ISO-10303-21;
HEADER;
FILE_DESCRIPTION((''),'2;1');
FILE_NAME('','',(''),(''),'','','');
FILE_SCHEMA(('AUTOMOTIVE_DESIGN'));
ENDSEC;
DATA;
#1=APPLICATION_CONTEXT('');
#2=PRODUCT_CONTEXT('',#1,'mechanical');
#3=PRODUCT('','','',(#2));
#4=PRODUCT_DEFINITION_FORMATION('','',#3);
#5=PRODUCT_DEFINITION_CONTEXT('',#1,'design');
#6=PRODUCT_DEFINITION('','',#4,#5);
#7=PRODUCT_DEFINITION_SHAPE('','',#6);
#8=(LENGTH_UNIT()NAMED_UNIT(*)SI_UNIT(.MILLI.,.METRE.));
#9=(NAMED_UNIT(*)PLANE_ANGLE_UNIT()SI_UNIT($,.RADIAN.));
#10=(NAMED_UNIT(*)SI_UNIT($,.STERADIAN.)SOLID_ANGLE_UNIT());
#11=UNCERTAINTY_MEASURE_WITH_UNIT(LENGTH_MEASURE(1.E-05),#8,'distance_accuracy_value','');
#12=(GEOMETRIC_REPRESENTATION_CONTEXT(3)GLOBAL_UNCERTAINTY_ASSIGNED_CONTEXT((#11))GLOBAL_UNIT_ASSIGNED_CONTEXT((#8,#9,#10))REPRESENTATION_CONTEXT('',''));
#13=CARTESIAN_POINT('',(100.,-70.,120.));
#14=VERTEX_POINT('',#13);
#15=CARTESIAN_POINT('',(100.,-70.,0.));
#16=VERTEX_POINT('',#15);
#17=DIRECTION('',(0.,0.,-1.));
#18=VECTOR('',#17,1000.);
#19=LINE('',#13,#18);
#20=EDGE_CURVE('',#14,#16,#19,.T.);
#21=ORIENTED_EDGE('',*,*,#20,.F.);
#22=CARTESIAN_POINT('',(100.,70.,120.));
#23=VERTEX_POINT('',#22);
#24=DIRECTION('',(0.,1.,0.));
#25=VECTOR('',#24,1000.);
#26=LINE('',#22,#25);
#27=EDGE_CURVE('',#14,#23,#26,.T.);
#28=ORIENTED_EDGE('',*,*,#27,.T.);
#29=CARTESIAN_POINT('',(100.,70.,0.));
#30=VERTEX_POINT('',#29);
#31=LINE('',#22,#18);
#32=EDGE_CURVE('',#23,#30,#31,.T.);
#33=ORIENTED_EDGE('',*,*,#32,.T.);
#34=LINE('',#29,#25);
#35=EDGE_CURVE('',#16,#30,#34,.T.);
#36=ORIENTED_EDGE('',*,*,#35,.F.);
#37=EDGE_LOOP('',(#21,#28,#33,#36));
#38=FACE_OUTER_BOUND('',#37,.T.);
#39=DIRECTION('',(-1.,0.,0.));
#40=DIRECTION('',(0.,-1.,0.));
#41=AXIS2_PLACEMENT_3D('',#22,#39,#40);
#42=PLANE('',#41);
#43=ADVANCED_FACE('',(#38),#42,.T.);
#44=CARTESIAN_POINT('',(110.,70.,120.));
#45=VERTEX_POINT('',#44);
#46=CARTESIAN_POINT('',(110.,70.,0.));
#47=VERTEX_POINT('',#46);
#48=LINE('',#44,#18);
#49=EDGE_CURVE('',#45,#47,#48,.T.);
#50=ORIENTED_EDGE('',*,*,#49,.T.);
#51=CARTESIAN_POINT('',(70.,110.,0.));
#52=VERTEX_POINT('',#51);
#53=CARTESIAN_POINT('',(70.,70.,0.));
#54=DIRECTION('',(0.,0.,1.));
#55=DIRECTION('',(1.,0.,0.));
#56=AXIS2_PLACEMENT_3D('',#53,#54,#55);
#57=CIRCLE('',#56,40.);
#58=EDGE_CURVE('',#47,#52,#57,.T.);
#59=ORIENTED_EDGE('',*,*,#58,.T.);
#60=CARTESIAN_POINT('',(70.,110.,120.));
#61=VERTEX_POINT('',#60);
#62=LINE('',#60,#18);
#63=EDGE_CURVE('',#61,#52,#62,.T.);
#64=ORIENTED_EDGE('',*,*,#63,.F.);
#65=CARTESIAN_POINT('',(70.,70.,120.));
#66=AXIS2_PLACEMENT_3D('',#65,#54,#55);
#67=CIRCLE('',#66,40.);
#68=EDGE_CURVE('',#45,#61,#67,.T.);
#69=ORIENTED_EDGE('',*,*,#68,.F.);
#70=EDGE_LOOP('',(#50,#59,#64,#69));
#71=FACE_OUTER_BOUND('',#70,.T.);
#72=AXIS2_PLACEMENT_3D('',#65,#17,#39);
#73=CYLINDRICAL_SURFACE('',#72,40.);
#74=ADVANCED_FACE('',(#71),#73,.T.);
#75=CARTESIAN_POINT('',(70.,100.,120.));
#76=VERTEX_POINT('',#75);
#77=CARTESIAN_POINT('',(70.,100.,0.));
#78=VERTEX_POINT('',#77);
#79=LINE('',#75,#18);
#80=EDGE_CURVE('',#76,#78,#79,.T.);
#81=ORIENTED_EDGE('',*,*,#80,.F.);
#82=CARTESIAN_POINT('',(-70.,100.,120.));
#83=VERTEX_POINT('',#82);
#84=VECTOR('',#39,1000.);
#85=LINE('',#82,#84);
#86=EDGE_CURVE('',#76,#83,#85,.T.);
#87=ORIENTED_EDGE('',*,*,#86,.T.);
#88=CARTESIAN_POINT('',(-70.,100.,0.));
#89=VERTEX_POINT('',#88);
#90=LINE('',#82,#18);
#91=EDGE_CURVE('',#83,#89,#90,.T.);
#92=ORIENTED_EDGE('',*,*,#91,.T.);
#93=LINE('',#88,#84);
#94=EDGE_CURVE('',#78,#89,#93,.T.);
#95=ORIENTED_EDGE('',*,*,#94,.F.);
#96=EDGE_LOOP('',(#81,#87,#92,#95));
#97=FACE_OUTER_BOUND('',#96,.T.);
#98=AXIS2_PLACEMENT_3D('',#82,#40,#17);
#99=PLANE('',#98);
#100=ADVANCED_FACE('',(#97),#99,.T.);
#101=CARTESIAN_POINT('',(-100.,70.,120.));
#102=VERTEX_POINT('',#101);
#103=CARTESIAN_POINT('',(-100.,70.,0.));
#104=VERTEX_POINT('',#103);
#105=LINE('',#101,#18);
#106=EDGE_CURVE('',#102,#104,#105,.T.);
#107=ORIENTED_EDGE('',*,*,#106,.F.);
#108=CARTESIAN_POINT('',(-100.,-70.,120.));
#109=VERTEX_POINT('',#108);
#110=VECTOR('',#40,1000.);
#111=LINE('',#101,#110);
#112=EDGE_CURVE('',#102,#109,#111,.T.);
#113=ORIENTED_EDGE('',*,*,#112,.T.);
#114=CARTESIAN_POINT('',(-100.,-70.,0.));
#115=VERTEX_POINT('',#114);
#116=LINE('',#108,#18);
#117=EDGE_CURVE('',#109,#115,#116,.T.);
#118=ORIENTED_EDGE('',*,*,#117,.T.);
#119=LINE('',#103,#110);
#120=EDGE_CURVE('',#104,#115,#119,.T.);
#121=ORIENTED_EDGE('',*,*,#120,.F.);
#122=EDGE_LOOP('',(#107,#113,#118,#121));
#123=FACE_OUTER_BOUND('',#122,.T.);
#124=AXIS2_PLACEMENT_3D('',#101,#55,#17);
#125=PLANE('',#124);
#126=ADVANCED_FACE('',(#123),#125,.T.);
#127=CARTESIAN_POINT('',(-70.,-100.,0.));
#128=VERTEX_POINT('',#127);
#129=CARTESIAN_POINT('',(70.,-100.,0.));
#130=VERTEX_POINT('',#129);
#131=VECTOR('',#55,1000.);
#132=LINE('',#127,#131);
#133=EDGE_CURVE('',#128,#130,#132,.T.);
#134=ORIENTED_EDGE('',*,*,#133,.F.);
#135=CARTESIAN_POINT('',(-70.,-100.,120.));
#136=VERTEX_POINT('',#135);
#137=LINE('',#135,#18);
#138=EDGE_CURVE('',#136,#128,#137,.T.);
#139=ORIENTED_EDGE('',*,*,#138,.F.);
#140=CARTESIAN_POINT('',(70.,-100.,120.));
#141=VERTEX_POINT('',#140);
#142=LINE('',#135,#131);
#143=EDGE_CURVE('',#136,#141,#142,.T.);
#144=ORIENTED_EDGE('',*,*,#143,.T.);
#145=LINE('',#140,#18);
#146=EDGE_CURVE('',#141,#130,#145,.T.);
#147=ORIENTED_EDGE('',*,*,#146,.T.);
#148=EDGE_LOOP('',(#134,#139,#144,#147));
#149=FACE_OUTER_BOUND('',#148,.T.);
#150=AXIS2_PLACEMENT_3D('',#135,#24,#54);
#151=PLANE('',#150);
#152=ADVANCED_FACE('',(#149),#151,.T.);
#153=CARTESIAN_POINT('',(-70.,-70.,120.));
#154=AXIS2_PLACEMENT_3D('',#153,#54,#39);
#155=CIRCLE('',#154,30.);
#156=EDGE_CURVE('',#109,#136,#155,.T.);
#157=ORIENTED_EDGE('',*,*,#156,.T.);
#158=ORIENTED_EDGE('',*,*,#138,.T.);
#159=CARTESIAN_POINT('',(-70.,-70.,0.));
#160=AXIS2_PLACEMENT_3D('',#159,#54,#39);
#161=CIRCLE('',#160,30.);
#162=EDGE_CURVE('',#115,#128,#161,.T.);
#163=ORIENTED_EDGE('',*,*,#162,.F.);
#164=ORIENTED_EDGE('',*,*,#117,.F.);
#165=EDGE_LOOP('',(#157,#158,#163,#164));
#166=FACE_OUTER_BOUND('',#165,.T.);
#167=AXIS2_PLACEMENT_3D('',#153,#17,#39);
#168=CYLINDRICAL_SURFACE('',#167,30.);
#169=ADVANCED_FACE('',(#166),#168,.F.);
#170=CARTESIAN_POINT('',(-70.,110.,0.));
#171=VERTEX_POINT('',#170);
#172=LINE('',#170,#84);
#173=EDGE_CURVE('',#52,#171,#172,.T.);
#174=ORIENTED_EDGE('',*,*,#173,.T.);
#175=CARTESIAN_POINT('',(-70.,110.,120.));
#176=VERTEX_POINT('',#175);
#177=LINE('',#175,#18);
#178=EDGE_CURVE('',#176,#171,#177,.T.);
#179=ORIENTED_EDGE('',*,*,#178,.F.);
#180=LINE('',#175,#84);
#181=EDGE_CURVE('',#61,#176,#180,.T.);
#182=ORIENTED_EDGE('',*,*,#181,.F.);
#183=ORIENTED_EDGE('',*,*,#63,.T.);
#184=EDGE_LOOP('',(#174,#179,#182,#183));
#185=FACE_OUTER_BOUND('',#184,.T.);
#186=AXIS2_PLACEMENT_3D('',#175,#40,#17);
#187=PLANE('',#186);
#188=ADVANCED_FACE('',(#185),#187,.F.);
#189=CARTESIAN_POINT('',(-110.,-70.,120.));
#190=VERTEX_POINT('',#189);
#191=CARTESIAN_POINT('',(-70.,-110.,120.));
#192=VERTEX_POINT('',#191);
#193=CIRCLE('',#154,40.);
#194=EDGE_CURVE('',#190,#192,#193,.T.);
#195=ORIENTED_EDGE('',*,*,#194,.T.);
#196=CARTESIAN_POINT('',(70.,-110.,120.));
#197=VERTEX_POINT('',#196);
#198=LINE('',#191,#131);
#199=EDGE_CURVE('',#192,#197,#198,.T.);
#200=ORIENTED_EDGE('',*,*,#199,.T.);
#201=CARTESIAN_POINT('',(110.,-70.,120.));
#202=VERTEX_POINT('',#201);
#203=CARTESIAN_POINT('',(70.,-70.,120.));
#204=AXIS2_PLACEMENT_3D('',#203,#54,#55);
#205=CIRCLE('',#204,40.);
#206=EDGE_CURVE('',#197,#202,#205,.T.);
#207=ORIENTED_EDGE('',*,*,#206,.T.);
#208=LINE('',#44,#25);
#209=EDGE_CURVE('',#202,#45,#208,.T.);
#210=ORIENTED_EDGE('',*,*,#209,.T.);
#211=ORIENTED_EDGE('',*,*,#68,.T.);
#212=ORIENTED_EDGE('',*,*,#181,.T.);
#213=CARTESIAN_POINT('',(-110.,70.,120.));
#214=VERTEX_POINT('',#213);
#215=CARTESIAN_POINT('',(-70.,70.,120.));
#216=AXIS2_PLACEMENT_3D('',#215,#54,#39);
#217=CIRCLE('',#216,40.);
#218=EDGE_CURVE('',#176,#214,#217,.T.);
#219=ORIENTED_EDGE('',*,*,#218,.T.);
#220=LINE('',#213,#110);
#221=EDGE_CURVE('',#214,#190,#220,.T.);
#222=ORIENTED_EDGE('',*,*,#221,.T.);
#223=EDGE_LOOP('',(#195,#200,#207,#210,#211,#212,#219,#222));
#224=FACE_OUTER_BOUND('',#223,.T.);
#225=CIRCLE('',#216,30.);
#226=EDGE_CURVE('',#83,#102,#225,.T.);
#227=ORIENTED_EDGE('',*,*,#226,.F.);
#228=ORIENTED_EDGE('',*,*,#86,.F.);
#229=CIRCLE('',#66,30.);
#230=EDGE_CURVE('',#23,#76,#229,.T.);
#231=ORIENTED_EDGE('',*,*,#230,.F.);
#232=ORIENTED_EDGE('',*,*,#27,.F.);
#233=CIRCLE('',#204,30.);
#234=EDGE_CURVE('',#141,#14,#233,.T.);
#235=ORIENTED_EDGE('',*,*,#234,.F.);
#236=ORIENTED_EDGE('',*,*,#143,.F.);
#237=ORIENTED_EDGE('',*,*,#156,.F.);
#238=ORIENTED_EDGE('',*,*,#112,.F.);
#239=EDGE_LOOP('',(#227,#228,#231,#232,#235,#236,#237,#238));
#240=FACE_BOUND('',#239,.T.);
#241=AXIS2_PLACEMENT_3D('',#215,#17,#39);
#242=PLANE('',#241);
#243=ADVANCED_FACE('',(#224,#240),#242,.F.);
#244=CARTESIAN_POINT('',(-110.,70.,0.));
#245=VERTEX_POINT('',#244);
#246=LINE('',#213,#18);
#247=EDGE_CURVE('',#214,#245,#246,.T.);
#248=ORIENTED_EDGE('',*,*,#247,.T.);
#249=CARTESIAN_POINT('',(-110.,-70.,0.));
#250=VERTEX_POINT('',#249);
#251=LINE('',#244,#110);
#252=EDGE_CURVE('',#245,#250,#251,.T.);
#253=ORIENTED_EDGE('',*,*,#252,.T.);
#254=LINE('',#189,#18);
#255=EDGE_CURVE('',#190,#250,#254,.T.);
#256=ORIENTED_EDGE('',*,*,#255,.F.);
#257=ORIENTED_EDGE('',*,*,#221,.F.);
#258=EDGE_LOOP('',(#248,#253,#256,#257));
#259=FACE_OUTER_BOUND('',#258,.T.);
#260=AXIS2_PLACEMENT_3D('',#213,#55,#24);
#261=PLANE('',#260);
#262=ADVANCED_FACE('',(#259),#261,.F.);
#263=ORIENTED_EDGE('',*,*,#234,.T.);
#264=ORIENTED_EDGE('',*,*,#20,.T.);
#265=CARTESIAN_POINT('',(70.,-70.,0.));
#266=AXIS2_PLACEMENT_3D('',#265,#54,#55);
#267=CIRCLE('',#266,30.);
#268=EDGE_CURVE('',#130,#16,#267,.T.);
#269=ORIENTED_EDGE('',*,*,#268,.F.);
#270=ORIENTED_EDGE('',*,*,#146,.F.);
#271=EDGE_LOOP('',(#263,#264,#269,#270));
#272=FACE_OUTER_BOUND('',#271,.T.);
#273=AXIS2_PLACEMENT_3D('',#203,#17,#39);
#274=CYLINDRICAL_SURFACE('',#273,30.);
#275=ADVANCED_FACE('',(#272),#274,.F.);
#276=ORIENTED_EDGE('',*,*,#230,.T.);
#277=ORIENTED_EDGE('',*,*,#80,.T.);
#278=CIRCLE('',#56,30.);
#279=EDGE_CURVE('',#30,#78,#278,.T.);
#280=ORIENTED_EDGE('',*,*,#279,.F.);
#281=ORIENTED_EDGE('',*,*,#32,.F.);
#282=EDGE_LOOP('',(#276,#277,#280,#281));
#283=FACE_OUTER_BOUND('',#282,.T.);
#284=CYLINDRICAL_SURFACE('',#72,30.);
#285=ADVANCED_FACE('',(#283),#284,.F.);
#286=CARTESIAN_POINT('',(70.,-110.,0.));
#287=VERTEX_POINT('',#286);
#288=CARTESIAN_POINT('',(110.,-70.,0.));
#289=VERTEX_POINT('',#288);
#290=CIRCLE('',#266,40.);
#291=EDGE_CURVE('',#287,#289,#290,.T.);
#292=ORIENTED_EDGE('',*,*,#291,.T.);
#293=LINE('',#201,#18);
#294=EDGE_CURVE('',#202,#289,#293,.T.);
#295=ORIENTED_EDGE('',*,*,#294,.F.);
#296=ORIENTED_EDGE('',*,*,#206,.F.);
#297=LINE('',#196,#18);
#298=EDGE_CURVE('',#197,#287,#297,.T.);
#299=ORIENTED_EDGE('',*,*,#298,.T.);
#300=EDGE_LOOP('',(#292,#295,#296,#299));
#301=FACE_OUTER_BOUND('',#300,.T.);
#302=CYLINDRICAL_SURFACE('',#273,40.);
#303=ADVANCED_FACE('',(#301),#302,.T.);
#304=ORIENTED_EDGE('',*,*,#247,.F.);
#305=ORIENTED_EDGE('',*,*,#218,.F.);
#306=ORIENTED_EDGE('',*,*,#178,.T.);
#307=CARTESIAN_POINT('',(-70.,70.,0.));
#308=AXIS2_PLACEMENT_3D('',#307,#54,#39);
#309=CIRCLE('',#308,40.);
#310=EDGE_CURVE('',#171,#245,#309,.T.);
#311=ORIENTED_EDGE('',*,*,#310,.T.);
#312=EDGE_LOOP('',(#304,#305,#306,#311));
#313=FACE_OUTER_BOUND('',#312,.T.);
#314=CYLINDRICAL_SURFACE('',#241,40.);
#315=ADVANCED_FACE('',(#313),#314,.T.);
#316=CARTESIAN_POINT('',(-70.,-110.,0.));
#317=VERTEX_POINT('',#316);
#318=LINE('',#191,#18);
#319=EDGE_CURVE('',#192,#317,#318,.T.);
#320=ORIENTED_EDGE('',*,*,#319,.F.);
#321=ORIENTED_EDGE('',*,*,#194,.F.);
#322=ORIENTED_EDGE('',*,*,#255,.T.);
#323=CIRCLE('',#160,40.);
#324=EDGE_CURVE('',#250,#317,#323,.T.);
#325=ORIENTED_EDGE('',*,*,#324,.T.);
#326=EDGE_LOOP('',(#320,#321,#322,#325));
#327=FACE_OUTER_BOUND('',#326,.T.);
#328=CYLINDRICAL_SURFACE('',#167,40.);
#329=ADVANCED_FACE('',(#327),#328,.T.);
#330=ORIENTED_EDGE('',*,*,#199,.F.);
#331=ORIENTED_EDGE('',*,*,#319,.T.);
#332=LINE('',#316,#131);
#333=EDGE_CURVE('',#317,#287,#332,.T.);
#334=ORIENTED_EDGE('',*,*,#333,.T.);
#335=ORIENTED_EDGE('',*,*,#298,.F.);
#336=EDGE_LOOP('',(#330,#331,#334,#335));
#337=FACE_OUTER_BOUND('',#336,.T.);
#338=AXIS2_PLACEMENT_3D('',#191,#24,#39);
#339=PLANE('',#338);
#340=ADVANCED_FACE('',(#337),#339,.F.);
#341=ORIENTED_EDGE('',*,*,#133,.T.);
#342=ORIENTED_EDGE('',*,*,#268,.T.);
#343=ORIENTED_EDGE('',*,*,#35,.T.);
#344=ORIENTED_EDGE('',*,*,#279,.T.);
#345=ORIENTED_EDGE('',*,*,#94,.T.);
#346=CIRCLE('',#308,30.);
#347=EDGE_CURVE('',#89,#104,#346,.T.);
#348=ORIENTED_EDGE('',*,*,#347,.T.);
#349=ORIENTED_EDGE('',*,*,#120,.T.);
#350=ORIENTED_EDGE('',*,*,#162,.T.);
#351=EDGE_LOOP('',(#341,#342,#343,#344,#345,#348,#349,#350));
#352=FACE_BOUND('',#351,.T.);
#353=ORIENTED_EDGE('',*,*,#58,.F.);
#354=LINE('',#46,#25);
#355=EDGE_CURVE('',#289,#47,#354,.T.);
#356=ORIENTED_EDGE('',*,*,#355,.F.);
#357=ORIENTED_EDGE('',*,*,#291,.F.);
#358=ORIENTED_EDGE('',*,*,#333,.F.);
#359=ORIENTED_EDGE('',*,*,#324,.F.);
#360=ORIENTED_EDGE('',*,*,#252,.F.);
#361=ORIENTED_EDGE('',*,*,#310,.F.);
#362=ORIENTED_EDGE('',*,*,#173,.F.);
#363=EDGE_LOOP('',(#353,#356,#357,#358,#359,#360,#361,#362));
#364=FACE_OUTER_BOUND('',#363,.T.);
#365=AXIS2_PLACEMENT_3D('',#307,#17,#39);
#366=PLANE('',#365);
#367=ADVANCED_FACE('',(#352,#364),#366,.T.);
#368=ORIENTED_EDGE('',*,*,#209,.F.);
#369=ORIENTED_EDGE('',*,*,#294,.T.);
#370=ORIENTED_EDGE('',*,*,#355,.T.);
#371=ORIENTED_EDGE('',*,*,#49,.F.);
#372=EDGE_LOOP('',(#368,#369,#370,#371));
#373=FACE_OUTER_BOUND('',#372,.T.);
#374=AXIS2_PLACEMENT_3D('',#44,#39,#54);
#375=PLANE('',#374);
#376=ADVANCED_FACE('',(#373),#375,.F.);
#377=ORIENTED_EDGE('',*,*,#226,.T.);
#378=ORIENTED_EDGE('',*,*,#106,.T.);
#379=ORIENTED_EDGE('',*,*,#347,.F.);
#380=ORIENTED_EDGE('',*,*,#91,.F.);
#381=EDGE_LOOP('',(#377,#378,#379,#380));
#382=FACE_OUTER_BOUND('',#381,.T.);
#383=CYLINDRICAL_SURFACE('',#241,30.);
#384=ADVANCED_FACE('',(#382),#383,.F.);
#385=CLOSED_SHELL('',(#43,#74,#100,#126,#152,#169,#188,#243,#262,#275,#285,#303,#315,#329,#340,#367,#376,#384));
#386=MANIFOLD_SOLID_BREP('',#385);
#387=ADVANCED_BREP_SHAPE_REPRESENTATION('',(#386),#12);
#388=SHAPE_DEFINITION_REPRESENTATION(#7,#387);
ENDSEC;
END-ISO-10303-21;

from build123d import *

# Parameters (mm, degrees)
EXTRUDE_1_DEPTH = 120


with BuildPart() as part:
    # 草图1 → 凸台-拉伸1 (new body)
    with BuildSketch(Plane.XY):
        with BuildLine():
            Line((-70, 110), (70, 110))
            ThreePointArc((70, 110), (98.284271247, 98.284271247), (110, 70))
            Line((110, 70), (110, -70))
            ThreePointArc((110, -70), (98.284271247, -98.284271247), (70, -110))
            Line((70, -110), (-70, -110))
            ThreePointArc((-70, -110), (-98.284271247, -98.284271247), (-110, -70))
            Line((-110, -70), (-110, 70))
            ThreePointArc((-110, 70), (-98.284271247, 98.284271247), (-70, 110))
        make_face()
        with BuildLine():
            Line((-70, 100), (70, 100))
            ThreePointArc((70, 100), (91.213203436, 91.213203436), (100, 70))
            Line((100, 70), (100, -70))
            ThreePointArc((100, -70), (91.213203436, -91.213203436), (70, -100))
            Line((70, -100), (-70, -100))
            ThreePointArc((-70, -100), (-91.213203436, -91.213203436), (-100, -70))
            Line((-100, -70), (-100, 70))
            ThreePointArc((-100, 70), (-91.213203436, 91.213203436), (-70, 100))
        make_face(mode=Mode.SUBTRACT)
    extrude(amount=EXTRUDE_1_DEPTH)


solid = part.part
